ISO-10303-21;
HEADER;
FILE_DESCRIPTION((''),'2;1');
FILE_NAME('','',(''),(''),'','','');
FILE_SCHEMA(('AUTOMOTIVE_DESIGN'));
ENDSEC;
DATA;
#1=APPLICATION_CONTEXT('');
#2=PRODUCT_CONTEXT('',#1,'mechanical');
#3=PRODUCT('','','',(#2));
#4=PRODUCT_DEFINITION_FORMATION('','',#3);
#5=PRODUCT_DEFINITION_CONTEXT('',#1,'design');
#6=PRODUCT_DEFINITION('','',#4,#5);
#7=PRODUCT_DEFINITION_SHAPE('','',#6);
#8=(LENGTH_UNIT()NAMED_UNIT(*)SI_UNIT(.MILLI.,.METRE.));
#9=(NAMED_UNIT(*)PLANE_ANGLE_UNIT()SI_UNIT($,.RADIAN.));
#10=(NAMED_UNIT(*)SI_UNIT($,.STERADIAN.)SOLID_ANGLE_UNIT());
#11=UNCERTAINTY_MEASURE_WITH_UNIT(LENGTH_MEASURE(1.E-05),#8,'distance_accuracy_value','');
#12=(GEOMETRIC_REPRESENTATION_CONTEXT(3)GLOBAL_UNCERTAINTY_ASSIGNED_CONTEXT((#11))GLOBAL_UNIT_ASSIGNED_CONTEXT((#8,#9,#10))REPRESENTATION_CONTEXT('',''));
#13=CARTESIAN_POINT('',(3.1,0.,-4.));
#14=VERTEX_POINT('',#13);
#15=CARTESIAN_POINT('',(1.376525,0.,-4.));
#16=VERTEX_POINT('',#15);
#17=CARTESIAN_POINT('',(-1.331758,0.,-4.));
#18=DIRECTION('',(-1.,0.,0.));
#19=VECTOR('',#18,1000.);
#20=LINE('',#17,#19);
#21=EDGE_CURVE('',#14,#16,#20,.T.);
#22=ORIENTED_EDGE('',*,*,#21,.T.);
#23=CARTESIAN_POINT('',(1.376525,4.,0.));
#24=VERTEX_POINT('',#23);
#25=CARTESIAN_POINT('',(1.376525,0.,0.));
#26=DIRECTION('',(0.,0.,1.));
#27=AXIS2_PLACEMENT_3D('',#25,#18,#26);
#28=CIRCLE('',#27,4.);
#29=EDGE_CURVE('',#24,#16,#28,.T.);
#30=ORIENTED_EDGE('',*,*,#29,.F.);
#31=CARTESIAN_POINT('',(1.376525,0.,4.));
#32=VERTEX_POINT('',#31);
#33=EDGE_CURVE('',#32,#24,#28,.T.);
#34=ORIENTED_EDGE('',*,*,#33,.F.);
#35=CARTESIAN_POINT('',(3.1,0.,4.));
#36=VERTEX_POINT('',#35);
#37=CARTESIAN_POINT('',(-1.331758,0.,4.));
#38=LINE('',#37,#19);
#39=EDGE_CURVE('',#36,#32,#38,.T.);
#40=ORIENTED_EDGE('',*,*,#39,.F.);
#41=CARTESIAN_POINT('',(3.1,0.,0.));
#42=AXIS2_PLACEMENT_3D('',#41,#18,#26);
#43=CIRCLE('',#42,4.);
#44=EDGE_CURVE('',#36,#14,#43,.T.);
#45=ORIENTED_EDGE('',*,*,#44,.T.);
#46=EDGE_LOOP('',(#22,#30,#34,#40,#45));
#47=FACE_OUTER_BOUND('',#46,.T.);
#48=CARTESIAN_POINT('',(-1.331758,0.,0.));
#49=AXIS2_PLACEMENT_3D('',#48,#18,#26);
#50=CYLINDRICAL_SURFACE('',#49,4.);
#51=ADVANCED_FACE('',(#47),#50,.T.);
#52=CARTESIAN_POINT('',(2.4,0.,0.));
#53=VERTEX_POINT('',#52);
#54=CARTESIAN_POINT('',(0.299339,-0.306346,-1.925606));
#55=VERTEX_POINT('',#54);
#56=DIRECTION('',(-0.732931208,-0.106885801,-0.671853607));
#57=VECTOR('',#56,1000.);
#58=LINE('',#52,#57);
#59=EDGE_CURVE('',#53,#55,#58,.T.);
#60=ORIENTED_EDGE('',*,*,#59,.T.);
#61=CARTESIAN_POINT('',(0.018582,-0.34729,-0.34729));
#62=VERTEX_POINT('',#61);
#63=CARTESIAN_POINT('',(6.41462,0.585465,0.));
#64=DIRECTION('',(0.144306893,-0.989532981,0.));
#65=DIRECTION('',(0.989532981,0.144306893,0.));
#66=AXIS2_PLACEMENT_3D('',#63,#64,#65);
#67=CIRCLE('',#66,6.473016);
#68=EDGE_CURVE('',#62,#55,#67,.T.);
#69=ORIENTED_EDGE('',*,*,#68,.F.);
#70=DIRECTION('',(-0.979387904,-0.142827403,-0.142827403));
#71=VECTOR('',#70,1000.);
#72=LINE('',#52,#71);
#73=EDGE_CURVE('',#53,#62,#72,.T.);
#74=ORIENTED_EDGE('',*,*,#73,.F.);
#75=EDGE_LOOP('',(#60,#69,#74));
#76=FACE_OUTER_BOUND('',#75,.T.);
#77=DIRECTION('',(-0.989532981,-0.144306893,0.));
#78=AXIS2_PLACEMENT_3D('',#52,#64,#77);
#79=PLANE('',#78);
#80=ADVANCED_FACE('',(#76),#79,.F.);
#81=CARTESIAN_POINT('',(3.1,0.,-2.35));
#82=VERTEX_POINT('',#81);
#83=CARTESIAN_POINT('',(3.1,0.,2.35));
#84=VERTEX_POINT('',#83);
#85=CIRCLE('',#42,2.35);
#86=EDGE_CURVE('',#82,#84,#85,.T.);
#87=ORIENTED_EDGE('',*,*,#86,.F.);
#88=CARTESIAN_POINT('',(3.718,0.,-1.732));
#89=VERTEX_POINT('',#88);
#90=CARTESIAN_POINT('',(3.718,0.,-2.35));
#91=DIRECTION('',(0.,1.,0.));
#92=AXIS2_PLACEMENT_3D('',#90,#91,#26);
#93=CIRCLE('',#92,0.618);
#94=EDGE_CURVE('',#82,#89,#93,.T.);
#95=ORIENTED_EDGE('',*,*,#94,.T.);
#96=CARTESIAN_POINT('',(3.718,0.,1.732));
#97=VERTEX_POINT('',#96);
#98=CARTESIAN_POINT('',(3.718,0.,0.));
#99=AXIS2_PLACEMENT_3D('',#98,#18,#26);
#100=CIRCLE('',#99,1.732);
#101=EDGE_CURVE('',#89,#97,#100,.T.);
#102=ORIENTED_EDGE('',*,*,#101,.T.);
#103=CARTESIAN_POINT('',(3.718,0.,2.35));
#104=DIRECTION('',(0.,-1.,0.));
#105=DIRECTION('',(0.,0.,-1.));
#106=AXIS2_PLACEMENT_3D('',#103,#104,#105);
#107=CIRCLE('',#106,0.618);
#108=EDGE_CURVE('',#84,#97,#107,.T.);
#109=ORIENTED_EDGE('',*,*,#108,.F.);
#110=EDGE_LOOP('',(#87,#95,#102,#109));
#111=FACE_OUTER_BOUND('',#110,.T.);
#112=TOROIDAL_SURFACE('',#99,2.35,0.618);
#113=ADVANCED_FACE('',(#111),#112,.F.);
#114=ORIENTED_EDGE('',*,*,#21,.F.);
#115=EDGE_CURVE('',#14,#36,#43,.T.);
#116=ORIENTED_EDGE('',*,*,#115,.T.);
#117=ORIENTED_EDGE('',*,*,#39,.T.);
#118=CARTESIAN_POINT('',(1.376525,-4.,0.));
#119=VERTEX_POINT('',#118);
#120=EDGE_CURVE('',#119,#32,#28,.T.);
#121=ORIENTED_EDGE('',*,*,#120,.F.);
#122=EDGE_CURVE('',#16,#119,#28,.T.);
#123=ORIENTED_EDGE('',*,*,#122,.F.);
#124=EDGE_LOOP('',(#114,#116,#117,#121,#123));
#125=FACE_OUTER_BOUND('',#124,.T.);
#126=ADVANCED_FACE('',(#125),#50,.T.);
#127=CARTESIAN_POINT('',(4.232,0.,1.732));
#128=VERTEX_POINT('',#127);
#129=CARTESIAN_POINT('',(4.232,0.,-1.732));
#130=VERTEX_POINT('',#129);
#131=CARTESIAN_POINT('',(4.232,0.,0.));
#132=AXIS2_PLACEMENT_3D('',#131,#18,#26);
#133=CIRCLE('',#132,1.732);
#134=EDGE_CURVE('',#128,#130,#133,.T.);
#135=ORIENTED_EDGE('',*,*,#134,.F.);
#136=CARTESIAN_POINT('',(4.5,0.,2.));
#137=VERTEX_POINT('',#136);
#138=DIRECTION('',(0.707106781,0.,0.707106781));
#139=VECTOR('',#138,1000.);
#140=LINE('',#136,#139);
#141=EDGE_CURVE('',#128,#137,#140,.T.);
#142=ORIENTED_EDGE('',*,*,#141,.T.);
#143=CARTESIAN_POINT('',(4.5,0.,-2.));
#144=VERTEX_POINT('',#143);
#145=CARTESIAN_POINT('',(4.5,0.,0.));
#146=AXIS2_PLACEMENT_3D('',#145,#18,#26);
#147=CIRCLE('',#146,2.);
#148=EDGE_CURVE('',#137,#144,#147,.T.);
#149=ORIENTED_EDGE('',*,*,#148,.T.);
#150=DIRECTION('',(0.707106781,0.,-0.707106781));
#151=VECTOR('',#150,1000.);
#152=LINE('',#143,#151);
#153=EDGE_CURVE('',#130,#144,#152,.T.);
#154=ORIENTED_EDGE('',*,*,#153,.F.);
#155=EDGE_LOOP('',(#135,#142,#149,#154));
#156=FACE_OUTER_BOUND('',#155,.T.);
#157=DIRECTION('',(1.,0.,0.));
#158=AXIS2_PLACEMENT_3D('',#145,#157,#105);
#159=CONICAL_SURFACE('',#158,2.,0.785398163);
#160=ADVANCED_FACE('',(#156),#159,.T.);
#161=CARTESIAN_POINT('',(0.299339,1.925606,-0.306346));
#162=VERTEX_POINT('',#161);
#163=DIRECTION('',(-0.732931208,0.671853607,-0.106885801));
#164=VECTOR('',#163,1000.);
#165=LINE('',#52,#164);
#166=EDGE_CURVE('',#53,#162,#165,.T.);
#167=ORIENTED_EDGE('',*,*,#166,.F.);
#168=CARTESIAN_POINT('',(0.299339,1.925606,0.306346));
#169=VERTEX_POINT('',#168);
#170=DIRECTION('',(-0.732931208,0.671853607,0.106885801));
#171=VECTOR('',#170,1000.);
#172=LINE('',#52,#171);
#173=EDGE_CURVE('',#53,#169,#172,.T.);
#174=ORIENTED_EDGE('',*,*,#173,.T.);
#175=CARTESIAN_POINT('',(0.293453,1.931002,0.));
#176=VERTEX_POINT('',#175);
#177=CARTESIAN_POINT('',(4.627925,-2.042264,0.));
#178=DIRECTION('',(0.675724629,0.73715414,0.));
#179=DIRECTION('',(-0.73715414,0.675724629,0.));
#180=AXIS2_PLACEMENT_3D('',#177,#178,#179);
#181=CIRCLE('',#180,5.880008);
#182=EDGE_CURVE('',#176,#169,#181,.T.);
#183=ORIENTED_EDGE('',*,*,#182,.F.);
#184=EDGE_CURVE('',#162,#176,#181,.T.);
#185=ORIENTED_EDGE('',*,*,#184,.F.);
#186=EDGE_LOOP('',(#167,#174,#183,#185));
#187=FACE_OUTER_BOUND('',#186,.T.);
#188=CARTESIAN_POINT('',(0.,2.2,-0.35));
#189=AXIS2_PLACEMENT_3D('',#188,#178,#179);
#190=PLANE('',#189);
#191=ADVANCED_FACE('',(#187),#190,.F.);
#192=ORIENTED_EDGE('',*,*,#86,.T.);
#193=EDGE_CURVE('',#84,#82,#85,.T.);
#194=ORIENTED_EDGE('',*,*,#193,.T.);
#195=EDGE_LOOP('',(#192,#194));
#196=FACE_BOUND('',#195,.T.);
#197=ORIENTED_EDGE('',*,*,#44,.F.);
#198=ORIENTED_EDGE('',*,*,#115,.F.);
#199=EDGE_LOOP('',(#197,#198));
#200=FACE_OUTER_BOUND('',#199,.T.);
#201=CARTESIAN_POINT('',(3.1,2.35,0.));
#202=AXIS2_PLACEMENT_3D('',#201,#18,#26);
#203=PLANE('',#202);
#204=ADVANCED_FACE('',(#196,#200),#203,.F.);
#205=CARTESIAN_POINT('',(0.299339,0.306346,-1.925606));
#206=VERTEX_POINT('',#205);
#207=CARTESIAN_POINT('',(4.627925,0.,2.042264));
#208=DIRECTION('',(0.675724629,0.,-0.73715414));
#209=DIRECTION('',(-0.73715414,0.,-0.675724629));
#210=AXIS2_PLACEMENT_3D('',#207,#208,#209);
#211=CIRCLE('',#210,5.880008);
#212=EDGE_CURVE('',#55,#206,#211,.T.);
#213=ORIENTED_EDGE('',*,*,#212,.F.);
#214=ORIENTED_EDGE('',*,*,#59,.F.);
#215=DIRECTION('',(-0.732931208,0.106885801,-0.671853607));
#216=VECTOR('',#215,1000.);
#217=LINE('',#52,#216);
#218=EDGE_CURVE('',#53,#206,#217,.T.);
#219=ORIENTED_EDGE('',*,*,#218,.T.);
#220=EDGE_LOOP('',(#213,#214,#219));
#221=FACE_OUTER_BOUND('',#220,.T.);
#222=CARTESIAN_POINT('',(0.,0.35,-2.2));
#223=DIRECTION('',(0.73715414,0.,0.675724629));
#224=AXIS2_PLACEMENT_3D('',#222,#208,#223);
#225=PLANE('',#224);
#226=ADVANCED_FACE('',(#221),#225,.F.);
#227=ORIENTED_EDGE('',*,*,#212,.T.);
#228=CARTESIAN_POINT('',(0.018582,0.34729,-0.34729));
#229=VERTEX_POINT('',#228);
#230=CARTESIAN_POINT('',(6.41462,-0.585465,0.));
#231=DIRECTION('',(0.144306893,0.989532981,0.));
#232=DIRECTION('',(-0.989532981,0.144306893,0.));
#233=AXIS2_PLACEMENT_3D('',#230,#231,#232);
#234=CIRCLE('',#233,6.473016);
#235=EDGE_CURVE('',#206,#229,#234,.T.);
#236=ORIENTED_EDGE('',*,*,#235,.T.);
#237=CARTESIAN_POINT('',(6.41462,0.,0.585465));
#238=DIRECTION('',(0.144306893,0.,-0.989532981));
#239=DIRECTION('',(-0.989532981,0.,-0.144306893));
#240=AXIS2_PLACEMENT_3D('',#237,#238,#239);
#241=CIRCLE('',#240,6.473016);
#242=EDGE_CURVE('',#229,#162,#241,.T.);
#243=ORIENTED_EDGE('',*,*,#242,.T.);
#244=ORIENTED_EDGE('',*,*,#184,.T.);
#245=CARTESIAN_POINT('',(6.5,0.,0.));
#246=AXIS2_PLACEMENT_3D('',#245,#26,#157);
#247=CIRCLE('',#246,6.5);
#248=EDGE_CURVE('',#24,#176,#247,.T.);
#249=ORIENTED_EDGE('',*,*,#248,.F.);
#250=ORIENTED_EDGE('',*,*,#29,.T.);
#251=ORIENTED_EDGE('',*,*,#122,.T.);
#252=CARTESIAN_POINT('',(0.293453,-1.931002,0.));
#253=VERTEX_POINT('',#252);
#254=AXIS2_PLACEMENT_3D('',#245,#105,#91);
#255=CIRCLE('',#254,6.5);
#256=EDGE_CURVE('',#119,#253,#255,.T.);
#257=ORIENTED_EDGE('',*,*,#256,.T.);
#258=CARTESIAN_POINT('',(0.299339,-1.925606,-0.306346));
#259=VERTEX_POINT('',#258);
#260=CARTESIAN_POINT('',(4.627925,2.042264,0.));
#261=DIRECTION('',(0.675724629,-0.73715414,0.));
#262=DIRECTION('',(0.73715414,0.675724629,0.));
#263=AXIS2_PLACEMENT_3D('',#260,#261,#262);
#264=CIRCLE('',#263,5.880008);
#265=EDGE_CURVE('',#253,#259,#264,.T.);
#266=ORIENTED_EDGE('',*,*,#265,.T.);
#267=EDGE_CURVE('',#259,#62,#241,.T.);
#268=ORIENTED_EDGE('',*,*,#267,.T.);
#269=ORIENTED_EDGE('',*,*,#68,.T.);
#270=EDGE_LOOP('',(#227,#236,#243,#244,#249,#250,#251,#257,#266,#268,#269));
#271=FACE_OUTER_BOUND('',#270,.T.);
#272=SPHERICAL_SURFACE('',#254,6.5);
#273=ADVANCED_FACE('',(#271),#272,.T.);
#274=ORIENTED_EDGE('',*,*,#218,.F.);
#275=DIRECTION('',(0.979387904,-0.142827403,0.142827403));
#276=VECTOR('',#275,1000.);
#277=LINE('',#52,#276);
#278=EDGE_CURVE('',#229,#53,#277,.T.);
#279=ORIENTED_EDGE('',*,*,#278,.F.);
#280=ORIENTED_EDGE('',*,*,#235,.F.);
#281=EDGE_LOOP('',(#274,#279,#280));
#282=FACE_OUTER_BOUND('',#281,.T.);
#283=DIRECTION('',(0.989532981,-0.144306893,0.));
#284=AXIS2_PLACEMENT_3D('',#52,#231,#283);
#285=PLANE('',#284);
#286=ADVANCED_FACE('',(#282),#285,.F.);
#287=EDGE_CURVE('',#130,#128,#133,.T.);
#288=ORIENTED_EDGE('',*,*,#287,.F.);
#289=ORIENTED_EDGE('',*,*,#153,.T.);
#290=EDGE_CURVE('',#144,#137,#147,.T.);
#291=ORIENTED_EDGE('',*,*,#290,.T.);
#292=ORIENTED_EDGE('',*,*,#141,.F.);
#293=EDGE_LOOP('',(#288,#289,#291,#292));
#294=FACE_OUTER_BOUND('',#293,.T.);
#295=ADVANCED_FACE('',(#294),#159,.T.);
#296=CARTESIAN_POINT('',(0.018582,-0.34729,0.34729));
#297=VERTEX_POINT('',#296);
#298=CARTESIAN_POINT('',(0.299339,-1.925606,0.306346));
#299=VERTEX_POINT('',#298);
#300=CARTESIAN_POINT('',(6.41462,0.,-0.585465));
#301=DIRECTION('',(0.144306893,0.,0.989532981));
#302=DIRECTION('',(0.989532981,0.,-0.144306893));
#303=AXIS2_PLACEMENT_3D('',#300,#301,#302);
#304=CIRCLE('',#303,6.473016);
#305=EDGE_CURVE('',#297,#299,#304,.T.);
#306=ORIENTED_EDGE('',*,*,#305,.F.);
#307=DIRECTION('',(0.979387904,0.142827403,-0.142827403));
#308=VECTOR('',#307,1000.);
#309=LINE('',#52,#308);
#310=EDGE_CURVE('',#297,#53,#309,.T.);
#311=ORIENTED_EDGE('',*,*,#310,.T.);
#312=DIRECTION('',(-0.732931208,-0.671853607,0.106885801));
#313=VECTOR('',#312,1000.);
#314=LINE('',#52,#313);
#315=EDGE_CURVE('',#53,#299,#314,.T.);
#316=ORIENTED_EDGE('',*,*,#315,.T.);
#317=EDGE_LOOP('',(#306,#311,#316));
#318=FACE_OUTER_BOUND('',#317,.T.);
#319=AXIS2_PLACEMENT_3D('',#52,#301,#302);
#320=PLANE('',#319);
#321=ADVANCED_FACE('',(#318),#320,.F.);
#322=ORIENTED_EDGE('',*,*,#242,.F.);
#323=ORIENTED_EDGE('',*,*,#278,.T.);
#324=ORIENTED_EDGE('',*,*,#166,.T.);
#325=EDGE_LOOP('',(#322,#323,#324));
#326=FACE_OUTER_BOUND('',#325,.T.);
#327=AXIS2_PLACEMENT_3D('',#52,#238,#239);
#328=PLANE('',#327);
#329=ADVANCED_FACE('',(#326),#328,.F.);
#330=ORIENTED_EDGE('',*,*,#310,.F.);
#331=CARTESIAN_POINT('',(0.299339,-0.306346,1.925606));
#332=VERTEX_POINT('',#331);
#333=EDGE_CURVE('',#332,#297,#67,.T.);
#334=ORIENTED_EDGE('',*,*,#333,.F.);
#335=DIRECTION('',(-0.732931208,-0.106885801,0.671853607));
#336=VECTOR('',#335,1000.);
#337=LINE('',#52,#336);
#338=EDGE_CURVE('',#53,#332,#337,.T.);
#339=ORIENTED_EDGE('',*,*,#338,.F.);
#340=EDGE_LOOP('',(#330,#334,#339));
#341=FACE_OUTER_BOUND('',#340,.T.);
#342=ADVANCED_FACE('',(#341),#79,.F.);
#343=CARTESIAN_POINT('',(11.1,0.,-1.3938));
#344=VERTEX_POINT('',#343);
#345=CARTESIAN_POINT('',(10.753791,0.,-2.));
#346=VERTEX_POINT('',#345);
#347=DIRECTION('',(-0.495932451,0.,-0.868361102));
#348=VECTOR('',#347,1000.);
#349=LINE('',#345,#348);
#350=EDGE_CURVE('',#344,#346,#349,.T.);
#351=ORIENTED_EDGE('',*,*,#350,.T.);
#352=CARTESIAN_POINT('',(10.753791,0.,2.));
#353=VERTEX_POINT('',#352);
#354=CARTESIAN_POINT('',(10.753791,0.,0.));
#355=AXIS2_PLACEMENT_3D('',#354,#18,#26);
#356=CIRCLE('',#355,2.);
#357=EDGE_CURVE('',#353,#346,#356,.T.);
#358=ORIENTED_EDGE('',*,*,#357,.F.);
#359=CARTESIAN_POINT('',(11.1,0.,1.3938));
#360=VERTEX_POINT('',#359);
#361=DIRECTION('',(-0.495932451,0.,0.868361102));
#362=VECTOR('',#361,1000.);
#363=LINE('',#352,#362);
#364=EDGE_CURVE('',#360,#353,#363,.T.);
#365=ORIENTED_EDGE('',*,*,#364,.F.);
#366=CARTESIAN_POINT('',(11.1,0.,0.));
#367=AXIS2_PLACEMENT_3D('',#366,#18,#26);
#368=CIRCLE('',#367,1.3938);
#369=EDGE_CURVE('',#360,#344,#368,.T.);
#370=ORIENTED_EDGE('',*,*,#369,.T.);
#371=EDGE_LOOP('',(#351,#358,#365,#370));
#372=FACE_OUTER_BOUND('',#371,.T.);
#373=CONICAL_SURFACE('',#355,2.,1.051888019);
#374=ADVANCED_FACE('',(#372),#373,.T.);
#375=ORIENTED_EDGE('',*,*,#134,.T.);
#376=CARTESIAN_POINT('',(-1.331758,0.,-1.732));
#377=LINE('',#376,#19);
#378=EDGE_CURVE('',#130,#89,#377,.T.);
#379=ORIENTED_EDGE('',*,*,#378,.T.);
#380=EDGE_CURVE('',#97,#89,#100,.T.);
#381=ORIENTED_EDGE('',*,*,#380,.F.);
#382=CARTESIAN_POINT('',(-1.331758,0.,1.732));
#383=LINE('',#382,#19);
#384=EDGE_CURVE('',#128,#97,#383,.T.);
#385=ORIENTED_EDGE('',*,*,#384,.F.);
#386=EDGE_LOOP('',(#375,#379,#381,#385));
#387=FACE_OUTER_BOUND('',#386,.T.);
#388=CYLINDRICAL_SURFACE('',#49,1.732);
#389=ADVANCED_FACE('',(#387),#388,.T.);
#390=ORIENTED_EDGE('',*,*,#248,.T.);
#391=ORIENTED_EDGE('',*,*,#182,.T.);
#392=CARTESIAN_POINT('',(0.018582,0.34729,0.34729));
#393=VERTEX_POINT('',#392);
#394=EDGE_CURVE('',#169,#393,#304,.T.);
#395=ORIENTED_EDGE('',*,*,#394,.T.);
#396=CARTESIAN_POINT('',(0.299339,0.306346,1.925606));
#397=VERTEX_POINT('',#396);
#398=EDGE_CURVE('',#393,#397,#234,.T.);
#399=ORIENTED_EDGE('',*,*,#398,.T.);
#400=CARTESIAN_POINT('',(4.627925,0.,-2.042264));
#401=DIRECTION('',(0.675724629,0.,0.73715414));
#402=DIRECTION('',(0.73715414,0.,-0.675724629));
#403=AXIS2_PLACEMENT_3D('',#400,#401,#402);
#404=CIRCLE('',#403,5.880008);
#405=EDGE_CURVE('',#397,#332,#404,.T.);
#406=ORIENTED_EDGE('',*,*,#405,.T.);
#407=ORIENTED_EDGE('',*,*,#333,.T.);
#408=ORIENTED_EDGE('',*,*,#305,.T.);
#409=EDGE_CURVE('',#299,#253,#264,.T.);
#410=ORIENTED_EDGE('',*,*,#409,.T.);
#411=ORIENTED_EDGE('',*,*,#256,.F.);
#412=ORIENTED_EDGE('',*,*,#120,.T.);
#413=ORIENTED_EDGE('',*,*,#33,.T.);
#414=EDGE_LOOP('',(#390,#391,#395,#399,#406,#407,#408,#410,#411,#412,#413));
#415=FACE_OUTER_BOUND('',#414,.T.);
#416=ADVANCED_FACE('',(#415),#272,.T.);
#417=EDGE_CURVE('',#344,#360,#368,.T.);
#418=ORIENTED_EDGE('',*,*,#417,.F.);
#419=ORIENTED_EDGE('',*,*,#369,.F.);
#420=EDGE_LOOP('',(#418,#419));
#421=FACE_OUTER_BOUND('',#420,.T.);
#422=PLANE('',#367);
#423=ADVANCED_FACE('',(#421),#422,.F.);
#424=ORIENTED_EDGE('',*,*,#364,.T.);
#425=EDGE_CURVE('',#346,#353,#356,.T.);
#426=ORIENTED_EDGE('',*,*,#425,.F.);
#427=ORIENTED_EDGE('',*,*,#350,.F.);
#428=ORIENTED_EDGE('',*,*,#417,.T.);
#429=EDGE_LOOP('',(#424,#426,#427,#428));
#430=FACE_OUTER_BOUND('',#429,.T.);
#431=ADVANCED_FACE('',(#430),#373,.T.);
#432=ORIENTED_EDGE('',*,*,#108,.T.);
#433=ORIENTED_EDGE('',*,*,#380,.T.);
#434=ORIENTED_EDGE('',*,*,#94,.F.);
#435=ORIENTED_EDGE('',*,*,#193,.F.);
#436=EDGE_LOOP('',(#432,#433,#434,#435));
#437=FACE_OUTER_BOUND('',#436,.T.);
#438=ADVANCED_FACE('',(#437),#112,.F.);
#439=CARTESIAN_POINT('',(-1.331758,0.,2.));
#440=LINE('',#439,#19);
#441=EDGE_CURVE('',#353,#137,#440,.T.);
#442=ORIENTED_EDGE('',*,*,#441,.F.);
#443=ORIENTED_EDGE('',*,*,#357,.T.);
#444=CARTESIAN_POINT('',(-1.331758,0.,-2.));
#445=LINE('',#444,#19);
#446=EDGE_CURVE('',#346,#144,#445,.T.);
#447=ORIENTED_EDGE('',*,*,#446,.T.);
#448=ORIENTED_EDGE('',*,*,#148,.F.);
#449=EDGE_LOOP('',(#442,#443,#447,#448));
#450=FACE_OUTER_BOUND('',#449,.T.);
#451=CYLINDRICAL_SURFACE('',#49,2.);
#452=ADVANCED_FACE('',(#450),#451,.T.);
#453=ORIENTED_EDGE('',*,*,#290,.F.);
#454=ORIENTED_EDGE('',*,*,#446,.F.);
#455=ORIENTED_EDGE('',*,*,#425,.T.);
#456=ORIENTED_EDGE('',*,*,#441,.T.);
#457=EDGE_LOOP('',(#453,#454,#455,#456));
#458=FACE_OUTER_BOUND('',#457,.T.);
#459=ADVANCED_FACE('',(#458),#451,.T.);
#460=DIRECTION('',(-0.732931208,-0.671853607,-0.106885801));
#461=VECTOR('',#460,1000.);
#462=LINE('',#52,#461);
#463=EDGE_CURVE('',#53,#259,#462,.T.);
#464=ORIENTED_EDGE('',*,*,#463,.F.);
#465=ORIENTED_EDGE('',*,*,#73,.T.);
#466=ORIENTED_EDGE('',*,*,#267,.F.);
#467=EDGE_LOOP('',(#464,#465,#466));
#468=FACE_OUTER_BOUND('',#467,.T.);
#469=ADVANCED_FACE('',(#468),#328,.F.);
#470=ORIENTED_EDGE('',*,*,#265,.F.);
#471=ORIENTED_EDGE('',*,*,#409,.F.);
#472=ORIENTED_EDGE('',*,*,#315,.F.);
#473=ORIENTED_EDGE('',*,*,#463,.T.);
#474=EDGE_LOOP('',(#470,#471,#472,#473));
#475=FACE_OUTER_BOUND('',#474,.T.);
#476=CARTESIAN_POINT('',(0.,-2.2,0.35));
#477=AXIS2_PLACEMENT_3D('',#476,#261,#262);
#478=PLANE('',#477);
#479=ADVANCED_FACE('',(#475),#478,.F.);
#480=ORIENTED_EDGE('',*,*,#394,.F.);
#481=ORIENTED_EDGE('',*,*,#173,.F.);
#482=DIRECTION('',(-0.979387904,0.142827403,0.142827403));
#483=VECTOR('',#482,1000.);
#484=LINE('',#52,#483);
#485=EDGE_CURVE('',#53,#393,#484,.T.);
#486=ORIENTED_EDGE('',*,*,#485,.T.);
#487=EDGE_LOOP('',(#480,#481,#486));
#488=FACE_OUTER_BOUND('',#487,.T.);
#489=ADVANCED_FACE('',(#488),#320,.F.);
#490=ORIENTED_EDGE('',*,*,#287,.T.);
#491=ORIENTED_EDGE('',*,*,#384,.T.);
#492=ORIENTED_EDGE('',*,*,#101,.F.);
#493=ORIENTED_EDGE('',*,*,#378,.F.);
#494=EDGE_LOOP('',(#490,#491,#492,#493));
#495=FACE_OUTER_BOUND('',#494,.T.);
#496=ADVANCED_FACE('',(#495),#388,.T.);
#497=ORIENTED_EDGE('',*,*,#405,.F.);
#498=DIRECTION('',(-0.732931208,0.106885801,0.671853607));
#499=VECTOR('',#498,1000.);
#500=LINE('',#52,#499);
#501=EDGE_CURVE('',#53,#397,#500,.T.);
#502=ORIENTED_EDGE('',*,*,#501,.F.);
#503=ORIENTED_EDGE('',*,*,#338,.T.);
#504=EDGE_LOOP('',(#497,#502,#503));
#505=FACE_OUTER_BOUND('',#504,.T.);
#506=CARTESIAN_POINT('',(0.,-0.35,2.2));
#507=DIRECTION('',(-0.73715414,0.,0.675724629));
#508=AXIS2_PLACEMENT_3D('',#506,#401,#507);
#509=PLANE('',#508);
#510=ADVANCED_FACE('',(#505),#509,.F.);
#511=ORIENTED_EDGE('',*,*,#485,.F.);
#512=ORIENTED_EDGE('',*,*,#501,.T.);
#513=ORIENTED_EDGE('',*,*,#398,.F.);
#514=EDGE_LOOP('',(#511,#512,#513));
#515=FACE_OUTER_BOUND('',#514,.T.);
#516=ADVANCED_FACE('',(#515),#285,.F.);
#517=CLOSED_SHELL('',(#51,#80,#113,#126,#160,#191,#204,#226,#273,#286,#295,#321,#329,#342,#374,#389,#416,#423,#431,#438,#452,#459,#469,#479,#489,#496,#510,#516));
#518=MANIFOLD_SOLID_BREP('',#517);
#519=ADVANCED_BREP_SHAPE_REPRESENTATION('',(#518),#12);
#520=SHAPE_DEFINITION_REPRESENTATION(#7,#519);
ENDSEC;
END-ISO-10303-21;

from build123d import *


with BuildPart() as part:
    # Sketch2 → Base-Revolve (revolve)
    with BuildSketch(Plane.XY, mode=Mode.PRIVATE) as base_revolve_sk:
        with BuildLine():
            Line((0, 0), (11.1, 0))
            Line((11.1, 0), (11.1, 2))
            Line((11.1, 2), (4.5, 2))
            Line((4.5, 2), (4.232, 1.732))
            Line((4.232, 1.732), (3.718, 1.732))
            ThreePointArc((3.718, 1.732), (3.281008009, 1.913008009), (3.1, 2.35))
            Line((3.1, 2.35), (3.1, 4))
            Line((3.1, 4), (1.376524617, 4))
            ThreePointArc((1.376524617, 4), (0.353757652, 2.115113473), (0, 0))
        make_face()
    revolve(base_revolve_sk.sketch.rotate(Axis((-1.331757704, 0, 0), (1, 0, 0)), 90), axis=Axis((-1.331757704, 0, 0), (1, 0, 0)))

    # Sketch3 → Cut-Revolve1 (revolve, cut)
    with BuildSketch(Plane.XY, mode=Mode.PRIVATE) as cut_revolve1_sk:
        Polygon((10.753791204, 2), (11.453791204, 2), (11.1, 1.3938), align=None)
    revolve(cut_revolve1_sk.sketch.rotate(Axis((-0.242766179, 0, 0), (1, 0, 0)), 90), axis=Axis((-0.242766179, 0, 0), (1, 0, 0)), mode=Mode.SUBTRACT)

    # Sketch5 → Cut-Loft1 section 0
    with BuildSketch(Plane(origin=(0, 0, 0), x_dir=(0, 0, -1), z_dir=(1, 0, 0)), mode=Mode.PRIVATE) as cut_loft1_s0:
        with BuildLine():
            Line((0.35, 2.2), (-0.35, 2.2))
            Line((-0.35, 2.2), (-0.35, -2.2))
            Line((-0.35, -2.2), (0.35, -2.2))
            Line((0.35, -2.2), (0.35, 2.2))
        make_face()
    cut_loft1 = loft([Vertex(2.4, 0, 0), cut_loft1_s0.sketch], mode=Mode.SUBTRACT)

    # Mirror1: Cut-Loft1 across plane
    add(cut_loft1.mirror(Plane(origin=(0, 0, 0), x_dir=(0, 0.7071067811865462, 0.7071067811865488), z_dir=(0, -0.7071067811865488, 0.7071067811865462))), mode=Mode.SUBTRACT)


solid = part.part
